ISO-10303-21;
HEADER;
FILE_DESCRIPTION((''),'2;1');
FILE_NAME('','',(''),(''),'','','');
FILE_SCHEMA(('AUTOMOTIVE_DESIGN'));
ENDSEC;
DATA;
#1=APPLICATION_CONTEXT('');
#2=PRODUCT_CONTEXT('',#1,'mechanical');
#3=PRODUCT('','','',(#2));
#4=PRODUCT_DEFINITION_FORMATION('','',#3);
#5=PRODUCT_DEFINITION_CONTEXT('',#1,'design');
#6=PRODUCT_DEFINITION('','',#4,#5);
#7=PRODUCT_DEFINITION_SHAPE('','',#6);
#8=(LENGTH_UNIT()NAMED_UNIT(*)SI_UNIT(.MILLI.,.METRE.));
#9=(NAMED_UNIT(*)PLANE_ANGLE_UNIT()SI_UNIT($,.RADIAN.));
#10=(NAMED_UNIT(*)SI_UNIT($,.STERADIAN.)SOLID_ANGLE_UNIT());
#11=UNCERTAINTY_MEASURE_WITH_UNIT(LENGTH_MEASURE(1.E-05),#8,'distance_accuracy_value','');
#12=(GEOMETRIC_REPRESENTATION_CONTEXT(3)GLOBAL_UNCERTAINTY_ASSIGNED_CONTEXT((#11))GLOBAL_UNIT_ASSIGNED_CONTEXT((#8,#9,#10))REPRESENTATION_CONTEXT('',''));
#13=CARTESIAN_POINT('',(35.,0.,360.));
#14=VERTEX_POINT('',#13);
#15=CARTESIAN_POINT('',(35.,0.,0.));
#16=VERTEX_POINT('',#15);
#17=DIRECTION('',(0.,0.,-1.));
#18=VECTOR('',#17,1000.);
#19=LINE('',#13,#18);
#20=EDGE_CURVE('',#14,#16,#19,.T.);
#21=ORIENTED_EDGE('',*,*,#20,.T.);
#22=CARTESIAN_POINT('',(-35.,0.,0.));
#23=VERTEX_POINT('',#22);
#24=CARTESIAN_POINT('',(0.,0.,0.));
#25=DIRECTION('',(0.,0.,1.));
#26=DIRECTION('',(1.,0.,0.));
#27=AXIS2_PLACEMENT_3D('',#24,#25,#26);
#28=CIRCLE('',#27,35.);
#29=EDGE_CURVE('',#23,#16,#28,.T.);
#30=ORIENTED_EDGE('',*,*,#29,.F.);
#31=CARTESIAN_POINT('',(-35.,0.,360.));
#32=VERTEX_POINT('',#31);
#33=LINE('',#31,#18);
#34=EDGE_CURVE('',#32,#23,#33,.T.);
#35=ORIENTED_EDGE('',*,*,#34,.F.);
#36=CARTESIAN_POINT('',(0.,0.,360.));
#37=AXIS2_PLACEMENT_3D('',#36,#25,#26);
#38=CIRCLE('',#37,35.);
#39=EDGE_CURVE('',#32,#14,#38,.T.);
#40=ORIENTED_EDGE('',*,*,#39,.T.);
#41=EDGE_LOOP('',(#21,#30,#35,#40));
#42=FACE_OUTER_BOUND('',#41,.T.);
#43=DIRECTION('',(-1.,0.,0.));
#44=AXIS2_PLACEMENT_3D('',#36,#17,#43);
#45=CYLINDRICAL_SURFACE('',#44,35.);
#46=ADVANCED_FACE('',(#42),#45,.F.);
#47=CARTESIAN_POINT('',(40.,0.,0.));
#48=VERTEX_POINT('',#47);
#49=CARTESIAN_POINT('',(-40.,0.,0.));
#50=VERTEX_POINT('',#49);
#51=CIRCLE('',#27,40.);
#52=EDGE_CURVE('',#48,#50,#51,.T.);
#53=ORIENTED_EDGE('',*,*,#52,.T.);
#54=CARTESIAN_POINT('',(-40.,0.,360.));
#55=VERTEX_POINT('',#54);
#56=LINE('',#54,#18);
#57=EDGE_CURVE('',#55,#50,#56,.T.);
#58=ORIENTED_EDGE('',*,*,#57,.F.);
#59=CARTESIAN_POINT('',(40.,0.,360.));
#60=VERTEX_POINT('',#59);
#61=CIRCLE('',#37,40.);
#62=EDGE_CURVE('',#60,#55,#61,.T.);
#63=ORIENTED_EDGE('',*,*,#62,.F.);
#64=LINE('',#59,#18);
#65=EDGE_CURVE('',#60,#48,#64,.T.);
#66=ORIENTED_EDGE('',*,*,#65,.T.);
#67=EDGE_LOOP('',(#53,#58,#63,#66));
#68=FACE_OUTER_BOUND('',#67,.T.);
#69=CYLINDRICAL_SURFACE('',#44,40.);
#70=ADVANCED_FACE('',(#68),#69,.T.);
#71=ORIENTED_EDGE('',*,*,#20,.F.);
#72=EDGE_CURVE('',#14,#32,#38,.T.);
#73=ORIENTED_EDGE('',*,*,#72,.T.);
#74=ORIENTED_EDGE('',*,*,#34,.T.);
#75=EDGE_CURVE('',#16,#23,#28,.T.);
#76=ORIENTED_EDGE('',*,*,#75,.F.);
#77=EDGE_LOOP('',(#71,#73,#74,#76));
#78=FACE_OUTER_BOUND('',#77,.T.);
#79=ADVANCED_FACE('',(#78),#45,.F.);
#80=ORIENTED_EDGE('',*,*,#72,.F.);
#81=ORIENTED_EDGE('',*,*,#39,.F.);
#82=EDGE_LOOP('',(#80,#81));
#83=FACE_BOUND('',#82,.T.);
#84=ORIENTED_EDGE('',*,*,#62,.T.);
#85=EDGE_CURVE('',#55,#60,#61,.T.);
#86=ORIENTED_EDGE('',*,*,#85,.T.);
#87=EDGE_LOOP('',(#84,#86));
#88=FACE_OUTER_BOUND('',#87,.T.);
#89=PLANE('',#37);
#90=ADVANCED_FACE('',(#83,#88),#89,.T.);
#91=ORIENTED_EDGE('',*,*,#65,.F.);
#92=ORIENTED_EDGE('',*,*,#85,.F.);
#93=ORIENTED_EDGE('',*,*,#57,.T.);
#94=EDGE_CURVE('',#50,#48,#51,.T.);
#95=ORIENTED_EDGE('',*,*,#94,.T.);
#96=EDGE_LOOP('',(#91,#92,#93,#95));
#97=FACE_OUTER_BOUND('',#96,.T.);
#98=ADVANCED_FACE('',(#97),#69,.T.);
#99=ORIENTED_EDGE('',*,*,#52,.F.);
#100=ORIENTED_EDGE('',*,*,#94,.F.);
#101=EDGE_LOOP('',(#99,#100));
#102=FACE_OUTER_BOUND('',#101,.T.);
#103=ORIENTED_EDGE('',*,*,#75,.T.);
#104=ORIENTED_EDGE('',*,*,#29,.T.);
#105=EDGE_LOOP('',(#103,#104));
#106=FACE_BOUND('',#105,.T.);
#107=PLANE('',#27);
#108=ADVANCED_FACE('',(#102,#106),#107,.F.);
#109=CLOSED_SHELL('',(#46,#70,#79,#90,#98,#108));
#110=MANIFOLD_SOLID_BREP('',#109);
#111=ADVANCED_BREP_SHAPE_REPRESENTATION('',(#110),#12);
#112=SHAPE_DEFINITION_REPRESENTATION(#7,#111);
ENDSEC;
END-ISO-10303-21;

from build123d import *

# Parameters (mm, degrees)
SKETCH_1_R      = 40
SKETCH_1_R_2    = 35
EXTRUDE_1_DEPTH = 360


with BuildPart() as part:
    # 草图1 → 凸台-拉伸1 (new body)
    with BuildSketch(Plane.XY):
        with Locations(Location((0, 0, 0), (0, 0, 180))):
            Circle(SKETCH_1_R)
        with Locations(Location((0, 0, 0), (0, 0, 180))):
            Circle(SKETCH_1_R_2, mode=Mode.SUBTRACT)
    extrude(amount=EXTRUDE_1_DEPTH)


solid = part.part
